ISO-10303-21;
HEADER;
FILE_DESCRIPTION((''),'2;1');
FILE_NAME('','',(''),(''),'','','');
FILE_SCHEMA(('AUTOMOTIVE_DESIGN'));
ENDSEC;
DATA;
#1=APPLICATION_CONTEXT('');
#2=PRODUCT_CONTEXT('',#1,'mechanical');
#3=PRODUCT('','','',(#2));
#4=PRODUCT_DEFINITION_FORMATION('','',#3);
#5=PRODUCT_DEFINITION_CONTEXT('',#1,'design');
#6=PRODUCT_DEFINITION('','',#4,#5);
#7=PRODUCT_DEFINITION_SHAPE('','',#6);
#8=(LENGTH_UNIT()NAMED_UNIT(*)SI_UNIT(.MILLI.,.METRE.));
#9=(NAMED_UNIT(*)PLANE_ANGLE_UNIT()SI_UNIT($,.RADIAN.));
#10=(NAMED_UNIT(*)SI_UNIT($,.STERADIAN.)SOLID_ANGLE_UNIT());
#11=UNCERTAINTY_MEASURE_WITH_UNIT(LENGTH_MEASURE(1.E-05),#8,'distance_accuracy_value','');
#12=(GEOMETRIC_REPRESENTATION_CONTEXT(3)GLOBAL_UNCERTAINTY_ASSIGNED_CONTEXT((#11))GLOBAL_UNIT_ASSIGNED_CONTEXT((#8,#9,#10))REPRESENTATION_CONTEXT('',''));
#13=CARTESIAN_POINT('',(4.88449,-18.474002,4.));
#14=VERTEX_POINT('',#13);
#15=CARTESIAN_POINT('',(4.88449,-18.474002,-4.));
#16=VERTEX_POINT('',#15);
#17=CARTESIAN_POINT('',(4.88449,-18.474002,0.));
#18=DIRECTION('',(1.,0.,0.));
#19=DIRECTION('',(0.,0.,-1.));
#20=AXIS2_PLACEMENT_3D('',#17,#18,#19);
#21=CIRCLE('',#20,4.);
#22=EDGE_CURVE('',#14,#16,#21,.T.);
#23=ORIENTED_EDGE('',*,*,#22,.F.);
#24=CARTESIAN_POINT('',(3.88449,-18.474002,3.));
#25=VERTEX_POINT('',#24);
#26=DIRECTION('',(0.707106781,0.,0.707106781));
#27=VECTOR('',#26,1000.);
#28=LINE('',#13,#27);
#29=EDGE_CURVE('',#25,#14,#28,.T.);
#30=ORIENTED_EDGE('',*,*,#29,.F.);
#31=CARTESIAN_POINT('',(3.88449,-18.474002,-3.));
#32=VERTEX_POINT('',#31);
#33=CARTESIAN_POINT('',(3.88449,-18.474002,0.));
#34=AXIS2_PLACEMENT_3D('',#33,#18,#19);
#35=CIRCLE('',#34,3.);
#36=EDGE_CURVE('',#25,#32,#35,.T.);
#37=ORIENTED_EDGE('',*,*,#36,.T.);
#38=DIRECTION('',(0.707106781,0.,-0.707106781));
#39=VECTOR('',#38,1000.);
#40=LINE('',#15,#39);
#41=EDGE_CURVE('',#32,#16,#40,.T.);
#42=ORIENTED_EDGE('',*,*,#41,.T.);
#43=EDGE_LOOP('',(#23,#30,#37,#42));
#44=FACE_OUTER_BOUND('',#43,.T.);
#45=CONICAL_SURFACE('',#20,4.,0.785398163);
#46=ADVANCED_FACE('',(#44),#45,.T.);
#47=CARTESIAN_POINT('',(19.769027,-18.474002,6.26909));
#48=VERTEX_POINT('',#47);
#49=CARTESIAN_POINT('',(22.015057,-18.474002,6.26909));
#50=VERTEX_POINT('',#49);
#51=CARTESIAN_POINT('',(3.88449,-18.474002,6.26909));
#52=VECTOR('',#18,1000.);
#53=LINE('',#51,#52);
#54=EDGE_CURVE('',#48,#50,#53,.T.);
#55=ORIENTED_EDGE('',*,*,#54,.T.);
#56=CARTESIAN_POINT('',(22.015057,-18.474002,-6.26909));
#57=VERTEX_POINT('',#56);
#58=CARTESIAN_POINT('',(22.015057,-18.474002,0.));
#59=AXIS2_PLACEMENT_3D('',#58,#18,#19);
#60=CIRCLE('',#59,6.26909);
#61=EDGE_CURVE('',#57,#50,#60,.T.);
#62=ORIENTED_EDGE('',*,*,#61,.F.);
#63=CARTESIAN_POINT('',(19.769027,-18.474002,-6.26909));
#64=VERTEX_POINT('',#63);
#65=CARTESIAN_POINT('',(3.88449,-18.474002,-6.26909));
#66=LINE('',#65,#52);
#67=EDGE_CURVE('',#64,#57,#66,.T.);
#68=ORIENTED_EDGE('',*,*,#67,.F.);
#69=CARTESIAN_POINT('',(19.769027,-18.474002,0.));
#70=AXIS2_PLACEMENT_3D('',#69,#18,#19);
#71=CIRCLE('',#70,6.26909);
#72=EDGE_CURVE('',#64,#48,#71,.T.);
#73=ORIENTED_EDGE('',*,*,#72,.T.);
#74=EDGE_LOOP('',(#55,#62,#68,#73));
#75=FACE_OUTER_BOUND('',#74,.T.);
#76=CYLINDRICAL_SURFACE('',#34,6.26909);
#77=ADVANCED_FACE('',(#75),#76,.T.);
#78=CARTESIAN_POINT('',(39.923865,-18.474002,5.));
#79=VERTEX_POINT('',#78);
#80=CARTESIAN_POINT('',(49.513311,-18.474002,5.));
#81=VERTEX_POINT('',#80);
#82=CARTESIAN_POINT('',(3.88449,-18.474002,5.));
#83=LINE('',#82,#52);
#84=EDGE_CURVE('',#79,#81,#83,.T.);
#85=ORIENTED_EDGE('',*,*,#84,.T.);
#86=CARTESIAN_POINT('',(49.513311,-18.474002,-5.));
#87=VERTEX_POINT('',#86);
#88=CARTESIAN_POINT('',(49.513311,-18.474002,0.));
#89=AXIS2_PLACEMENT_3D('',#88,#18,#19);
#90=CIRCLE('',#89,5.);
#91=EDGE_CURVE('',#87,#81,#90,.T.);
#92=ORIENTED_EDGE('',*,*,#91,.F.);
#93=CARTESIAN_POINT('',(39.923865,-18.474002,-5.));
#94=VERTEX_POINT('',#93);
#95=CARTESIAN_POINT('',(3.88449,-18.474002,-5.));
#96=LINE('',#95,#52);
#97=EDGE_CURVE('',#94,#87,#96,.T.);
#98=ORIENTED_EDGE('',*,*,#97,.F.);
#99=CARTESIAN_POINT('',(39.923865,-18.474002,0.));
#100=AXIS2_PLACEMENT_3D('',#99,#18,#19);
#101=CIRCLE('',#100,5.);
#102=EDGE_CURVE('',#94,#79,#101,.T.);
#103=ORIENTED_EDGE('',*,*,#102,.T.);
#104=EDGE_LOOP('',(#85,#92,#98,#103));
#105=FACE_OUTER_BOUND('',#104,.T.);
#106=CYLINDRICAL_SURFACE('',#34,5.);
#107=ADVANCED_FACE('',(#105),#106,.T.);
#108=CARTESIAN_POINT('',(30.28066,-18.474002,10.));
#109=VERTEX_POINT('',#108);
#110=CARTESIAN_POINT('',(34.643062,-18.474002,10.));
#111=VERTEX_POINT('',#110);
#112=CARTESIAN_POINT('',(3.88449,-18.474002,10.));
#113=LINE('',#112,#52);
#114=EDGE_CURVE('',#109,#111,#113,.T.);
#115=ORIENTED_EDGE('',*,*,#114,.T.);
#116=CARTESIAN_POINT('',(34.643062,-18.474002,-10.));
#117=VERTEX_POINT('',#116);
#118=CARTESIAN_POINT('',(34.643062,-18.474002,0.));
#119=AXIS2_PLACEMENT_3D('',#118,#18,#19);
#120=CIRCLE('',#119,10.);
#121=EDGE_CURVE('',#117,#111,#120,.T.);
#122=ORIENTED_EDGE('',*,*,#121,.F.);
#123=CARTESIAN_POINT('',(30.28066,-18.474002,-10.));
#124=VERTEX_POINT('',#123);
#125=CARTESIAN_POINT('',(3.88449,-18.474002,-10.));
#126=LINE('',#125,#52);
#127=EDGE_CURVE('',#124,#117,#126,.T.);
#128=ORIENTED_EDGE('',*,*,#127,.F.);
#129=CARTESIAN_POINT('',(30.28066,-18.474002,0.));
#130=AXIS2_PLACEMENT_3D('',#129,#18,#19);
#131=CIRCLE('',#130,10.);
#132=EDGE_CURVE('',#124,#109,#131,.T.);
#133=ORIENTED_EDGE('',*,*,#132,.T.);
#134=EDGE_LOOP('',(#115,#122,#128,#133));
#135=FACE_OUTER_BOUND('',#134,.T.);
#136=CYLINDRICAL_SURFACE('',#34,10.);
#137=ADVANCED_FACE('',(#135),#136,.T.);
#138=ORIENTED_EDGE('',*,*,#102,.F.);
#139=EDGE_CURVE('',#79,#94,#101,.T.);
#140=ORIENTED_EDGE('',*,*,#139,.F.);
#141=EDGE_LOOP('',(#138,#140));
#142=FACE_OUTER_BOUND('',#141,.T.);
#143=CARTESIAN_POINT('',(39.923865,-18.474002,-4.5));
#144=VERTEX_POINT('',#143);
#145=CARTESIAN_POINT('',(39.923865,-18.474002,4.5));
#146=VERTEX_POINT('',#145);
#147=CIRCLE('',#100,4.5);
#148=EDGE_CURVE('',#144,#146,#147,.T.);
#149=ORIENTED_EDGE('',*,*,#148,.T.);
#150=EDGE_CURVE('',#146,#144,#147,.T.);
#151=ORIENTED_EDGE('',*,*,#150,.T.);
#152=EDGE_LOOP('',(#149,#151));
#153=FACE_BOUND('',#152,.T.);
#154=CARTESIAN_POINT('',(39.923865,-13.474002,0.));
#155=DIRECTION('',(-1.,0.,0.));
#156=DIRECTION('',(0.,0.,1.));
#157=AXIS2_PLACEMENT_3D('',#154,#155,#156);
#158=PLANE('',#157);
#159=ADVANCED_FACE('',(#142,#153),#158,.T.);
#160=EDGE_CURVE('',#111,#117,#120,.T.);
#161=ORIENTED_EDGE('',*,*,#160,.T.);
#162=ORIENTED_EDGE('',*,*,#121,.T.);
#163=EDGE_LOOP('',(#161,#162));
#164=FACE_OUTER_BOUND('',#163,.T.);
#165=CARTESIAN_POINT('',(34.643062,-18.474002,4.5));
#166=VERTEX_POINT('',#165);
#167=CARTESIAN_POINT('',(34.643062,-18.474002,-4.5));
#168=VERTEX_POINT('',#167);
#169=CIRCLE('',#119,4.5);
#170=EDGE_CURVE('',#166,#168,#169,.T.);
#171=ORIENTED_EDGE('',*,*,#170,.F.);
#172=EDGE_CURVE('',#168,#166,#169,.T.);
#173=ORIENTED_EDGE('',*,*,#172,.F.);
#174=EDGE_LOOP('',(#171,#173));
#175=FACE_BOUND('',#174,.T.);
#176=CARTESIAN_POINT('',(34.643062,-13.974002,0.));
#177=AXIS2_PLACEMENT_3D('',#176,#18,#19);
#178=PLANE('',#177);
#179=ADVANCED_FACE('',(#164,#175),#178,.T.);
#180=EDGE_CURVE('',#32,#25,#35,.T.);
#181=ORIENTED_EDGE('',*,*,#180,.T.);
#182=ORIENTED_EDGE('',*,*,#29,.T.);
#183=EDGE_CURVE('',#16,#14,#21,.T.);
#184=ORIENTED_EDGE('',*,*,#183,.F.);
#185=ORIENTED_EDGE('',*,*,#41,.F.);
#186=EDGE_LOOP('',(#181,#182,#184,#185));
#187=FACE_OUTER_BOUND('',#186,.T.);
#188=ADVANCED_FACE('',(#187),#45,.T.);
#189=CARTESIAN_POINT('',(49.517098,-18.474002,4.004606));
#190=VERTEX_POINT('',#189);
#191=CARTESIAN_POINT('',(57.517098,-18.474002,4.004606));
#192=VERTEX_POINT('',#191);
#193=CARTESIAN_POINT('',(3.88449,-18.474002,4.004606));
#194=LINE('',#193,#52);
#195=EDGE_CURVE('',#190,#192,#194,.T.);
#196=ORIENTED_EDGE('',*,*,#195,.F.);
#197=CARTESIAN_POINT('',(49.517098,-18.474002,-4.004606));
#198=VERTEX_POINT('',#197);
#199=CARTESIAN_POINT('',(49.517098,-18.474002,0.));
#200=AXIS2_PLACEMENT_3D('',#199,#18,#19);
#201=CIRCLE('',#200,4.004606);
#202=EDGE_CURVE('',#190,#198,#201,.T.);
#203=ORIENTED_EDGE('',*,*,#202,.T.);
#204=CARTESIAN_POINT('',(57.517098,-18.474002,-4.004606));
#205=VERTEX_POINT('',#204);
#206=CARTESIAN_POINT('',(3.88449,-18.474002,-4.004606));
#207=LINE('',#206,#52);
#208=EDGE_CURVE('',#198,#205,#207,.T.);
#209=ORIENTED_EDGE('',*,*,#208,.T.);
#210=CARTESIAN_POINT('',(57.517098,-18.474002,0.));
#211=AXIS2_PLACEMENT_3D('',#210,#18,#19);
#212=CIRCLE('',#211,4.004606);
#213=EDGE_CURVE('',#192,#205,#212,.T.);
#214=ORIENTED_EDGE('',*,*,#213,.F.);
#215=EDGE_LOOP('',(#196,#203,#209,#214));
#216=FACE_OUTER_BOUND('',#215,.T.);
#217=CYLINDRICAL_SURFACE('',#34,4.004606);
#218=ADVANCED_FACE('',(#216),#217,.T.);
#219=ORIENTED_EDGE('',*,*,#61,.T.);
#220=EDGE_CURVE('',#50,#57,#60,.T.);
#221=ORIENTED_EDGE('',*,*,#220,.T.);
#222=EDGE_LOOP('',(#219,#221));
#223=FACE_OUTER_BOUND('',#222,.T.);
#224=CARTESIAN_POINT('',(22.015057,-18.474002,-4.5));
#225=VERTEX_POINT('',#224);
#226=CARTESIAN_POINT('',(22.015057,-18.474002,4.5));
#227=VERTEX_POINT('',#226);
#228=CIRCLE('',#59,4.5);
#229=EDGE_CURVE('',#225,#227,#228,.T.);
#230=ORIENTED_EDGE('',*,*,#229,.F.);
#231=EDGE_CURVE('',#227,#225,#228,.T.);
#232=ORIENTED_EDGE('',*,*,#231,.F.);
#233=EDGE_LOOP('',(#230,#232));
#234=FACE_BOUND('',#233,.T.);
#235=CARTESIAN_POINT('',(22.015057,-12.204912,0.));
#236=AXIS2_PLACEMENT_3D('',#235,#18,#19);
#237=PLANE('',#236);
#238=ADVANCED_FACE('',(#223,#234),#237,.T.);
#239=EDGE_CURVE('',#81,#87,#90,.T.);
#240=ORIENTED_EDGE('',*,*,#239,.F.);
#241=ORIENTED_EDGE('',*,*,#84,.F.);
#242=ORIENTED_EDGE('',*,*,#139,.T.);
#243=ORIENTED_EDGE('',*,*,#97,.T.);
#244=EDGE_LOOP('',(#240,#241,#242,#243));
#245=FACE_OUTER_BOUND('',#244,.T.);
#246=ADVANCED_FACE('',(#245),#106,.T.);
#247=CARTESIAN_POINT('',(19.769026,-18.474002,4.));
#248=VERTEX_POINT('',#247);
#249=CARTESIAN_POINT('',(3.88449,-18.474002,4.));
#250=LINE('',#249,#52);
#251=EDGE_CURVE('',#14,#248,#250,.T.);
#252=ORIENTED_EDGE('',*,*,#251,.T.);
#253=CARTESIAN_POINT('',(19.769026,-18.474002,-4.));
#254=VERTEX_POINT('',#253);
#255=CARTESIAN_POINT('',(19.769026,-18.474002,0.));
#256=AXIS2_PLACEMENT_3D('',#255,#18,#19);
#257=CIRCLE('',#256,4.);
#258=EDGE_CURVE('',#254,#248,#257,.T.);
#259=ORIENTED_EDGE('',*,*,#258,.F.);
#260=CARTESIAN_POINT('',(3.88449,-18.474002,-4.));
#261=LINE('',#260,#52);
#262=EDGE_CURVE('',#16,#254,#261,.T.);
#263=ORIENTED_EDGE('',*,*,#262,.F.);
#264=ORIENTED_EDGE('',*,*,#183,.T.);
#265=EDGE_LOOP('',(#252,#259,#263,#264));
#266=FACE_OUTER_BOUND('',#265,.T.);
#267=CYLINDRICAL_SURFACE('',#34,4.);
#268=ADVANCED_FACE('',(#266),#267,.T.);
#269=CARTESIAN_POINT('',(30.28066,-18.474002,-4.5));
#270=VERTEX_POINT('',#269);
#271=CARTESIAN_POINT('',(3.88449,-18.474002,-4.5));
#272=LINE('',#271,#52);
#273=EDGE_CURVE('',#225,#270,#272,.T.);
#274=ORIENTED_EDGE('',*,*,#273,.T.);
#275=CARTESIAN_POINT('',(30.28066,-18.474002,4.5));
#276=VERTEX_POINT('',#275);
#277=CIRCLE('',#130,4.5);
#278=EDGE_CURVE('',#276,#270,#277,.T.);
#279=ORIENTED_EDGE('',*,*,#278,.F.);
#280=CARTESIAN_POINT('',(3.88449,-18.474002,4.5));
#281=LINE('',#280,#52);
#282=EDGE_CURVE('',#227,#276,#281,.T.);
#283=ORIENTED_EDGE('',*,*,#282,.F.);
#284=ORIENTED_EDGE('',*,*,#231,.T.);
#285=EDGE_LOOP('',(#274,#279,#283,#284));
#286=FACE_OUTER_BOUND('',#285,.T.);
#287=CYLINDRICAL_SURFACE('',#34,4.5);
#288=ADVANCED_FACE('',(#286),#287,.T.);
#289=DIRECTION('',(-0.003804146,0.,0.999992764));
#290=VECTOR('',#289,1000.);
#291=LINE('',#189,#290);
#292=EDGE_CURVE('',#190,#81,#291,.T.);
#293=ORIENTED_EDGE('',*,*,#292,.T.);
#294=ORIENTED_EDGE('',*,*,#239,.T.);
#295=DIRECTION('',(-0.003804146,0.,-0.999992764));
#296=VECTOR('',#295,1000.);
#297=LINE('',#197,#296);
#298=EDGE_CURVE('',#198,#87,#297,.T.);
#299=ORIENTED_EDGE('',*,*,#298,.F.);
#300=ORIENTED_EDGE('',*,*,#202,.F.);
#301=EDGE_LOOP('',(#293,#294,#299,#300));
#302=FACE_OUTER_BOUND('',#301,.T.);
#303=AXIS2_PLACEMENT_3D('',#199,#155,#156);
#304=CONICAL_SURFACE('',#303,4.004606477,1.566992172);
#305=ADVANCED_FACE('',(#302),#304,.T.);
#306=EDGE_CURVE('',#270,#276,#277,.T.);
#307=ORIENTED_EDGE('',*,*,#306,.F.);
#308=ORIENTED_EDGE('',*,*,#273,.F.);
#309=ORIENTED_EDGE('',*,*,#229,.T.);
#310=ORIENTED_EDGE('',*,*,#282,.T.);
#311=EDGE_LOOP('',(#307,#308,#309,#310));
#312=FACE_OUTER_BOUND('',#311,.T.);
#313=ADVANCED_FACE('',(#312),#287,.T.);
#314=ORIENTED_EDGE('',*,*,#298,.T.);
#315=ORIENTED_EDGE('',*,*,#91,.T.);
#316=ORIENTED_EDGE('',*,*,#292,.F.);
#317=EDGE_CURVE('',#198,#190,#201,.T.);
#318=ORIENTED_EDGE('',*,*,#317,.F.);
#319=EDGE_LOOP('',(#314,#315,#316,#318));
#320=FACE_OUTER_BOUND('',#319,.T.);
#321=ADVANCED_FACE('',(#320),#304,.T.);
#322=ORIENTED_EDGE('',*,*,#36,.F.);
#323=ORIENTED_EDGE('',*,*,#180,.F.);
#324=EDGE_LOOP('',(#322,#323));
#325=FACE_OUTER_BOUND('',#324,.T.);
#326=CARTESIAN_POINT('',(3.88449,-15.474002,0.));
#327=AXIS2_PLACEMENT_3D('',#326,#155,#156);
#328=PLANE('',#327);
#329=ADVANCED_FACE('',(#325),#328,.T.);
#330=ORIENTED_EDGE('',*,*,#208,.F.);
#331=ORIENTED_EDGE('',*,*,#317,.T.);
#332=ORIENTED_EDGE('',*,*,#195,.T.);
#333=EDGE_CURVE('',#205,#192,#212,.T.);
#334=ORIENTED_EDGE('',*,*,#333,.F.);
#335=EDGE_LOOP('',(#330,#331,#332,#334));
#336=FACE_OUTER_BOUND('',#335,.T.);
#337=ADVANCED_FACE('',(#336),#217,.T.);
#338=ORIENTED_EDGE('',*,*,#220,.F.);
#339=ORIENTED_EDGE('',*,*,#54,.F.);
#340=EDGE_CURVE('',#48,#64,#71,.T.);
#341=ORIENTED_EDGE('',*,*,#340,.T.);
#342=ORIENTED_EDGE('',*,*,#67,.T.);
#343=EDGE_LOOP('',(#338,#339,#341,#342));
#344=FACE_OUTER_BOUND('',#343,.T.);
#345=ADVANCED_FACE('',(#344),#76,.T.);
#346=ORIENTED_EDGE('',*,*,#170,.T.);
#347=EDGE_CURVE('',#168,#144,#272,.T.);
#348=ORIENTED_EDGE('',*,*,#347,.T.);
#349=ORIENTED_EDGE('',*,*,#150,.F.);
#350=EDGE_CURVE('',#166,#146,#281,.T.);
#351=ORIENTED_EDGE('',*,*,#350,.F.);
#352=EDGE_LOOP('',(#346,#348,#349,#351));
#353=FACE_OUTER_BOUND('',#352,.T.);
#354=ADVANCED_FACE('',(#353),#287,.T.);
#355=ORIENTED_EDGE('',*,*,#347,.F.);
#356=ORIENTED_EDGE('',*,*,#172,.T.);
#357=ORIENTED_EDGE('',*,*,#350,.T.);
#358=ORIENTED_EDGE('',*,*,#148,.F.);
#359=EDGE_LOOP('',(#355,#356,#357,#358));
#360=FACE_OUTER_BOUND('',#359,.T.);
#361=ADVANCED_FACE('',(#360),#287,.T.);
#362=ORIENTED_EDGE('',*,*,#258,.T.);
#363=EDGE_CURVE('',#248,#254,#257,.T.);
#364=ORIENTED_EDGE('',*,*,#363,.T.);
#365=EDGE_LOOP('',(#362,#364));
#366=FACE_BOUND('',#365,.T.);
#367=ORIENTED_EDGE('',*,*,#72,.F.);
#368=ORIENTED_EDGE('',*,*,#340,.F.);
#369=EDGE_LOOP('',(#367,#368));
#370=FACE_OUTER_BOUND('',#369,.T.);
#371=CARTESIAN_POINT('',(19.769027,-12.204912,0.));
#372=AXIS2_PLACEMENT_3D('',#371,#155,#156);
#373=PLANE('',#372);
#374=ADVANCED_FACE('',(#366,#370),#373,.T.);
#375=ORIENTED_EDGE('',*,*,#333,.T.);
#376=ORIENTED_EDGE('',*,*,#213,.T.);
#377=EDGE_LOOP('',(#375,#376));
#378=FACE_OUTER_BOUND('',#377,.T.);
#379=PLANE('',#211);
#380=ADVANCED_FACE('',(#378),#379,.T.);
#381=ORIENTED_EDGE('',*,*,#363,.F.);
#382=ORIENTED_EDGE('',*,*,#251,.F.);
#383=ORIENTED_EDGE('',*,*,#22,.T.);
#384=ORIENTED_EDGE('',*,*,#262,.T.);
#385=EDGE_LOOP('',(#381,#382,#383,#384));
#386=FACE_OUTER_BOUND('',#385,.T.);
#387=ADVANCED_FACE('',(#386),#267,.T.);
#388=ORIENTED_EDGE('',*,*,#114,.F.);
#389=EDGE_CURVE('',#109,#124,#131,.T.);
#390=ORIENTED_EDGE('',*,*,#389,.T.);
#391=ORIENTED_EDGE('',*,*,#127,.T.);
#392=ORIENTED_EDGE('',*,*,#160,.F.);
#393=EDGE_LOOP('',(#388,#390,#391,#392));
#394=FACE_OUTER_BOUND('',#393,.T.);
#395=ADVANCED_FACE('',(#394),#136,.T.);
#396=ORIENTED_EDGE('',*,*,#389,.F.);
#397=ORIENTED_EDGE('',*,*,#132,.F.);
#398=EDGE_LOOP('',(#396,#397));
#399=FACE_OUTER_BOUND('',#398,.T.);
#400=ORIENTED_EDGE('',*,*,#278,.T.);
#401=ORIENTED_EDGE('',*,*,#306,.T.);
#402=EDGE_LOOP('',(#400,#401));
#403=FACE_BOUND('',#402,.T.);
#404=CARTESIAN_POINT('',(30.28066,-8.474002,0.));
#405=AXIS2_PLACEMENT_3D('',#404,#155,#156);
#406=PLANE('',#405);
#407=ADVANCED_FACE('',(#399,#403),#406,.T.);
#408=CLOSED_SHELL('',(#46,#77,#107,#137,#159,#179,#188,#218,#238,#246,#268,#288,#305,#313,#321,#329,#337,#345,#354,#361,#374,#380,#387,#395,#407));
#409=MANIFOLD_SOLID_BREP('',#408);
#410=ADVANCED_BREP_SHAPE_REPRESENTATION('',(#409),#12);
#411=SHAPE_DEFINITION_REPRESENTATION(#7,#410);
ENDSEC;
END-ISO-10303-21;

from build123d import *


with BuildPart() as part:
    # Model → Revolve1 (revolve)
    with BuildSketch(Plane.XY, mode=Mode.PRIVATE) as revolve1_sk:
        Polygon((49.51331086, -13.474001866), (49.517097509, -14.469395389), (57.517097509, -14.469395389), (57.517097509, -18.474001866), (3.884490088, -18.474001866), (3.884490088, -15.474001866), (4.884490088, -14.474001866), (11.769027201, -14.474001866), (19.769026262, -14.474001866), (19.769027201, -12.204912355), (22.015056766, -12.204912355), (22.015056766, -13.974001866), (30.280660424, -13.974001866), (30.280660424, -8.474001866), (34.643062355, -8.474001866), (34.643062355, -13.974001866), (39.923864692, -13.974001866), (39.923864692, -13.474001866), align=None)
    revolve(revolve1_sk.sketch.rotate(Axis((3.884490088, -18.474001866, 0), (-1, 0, 0)), 90), axis=Axis((3.884490088, -18.474001866, 0), (-1, 0, 0)))


solid = part.part
